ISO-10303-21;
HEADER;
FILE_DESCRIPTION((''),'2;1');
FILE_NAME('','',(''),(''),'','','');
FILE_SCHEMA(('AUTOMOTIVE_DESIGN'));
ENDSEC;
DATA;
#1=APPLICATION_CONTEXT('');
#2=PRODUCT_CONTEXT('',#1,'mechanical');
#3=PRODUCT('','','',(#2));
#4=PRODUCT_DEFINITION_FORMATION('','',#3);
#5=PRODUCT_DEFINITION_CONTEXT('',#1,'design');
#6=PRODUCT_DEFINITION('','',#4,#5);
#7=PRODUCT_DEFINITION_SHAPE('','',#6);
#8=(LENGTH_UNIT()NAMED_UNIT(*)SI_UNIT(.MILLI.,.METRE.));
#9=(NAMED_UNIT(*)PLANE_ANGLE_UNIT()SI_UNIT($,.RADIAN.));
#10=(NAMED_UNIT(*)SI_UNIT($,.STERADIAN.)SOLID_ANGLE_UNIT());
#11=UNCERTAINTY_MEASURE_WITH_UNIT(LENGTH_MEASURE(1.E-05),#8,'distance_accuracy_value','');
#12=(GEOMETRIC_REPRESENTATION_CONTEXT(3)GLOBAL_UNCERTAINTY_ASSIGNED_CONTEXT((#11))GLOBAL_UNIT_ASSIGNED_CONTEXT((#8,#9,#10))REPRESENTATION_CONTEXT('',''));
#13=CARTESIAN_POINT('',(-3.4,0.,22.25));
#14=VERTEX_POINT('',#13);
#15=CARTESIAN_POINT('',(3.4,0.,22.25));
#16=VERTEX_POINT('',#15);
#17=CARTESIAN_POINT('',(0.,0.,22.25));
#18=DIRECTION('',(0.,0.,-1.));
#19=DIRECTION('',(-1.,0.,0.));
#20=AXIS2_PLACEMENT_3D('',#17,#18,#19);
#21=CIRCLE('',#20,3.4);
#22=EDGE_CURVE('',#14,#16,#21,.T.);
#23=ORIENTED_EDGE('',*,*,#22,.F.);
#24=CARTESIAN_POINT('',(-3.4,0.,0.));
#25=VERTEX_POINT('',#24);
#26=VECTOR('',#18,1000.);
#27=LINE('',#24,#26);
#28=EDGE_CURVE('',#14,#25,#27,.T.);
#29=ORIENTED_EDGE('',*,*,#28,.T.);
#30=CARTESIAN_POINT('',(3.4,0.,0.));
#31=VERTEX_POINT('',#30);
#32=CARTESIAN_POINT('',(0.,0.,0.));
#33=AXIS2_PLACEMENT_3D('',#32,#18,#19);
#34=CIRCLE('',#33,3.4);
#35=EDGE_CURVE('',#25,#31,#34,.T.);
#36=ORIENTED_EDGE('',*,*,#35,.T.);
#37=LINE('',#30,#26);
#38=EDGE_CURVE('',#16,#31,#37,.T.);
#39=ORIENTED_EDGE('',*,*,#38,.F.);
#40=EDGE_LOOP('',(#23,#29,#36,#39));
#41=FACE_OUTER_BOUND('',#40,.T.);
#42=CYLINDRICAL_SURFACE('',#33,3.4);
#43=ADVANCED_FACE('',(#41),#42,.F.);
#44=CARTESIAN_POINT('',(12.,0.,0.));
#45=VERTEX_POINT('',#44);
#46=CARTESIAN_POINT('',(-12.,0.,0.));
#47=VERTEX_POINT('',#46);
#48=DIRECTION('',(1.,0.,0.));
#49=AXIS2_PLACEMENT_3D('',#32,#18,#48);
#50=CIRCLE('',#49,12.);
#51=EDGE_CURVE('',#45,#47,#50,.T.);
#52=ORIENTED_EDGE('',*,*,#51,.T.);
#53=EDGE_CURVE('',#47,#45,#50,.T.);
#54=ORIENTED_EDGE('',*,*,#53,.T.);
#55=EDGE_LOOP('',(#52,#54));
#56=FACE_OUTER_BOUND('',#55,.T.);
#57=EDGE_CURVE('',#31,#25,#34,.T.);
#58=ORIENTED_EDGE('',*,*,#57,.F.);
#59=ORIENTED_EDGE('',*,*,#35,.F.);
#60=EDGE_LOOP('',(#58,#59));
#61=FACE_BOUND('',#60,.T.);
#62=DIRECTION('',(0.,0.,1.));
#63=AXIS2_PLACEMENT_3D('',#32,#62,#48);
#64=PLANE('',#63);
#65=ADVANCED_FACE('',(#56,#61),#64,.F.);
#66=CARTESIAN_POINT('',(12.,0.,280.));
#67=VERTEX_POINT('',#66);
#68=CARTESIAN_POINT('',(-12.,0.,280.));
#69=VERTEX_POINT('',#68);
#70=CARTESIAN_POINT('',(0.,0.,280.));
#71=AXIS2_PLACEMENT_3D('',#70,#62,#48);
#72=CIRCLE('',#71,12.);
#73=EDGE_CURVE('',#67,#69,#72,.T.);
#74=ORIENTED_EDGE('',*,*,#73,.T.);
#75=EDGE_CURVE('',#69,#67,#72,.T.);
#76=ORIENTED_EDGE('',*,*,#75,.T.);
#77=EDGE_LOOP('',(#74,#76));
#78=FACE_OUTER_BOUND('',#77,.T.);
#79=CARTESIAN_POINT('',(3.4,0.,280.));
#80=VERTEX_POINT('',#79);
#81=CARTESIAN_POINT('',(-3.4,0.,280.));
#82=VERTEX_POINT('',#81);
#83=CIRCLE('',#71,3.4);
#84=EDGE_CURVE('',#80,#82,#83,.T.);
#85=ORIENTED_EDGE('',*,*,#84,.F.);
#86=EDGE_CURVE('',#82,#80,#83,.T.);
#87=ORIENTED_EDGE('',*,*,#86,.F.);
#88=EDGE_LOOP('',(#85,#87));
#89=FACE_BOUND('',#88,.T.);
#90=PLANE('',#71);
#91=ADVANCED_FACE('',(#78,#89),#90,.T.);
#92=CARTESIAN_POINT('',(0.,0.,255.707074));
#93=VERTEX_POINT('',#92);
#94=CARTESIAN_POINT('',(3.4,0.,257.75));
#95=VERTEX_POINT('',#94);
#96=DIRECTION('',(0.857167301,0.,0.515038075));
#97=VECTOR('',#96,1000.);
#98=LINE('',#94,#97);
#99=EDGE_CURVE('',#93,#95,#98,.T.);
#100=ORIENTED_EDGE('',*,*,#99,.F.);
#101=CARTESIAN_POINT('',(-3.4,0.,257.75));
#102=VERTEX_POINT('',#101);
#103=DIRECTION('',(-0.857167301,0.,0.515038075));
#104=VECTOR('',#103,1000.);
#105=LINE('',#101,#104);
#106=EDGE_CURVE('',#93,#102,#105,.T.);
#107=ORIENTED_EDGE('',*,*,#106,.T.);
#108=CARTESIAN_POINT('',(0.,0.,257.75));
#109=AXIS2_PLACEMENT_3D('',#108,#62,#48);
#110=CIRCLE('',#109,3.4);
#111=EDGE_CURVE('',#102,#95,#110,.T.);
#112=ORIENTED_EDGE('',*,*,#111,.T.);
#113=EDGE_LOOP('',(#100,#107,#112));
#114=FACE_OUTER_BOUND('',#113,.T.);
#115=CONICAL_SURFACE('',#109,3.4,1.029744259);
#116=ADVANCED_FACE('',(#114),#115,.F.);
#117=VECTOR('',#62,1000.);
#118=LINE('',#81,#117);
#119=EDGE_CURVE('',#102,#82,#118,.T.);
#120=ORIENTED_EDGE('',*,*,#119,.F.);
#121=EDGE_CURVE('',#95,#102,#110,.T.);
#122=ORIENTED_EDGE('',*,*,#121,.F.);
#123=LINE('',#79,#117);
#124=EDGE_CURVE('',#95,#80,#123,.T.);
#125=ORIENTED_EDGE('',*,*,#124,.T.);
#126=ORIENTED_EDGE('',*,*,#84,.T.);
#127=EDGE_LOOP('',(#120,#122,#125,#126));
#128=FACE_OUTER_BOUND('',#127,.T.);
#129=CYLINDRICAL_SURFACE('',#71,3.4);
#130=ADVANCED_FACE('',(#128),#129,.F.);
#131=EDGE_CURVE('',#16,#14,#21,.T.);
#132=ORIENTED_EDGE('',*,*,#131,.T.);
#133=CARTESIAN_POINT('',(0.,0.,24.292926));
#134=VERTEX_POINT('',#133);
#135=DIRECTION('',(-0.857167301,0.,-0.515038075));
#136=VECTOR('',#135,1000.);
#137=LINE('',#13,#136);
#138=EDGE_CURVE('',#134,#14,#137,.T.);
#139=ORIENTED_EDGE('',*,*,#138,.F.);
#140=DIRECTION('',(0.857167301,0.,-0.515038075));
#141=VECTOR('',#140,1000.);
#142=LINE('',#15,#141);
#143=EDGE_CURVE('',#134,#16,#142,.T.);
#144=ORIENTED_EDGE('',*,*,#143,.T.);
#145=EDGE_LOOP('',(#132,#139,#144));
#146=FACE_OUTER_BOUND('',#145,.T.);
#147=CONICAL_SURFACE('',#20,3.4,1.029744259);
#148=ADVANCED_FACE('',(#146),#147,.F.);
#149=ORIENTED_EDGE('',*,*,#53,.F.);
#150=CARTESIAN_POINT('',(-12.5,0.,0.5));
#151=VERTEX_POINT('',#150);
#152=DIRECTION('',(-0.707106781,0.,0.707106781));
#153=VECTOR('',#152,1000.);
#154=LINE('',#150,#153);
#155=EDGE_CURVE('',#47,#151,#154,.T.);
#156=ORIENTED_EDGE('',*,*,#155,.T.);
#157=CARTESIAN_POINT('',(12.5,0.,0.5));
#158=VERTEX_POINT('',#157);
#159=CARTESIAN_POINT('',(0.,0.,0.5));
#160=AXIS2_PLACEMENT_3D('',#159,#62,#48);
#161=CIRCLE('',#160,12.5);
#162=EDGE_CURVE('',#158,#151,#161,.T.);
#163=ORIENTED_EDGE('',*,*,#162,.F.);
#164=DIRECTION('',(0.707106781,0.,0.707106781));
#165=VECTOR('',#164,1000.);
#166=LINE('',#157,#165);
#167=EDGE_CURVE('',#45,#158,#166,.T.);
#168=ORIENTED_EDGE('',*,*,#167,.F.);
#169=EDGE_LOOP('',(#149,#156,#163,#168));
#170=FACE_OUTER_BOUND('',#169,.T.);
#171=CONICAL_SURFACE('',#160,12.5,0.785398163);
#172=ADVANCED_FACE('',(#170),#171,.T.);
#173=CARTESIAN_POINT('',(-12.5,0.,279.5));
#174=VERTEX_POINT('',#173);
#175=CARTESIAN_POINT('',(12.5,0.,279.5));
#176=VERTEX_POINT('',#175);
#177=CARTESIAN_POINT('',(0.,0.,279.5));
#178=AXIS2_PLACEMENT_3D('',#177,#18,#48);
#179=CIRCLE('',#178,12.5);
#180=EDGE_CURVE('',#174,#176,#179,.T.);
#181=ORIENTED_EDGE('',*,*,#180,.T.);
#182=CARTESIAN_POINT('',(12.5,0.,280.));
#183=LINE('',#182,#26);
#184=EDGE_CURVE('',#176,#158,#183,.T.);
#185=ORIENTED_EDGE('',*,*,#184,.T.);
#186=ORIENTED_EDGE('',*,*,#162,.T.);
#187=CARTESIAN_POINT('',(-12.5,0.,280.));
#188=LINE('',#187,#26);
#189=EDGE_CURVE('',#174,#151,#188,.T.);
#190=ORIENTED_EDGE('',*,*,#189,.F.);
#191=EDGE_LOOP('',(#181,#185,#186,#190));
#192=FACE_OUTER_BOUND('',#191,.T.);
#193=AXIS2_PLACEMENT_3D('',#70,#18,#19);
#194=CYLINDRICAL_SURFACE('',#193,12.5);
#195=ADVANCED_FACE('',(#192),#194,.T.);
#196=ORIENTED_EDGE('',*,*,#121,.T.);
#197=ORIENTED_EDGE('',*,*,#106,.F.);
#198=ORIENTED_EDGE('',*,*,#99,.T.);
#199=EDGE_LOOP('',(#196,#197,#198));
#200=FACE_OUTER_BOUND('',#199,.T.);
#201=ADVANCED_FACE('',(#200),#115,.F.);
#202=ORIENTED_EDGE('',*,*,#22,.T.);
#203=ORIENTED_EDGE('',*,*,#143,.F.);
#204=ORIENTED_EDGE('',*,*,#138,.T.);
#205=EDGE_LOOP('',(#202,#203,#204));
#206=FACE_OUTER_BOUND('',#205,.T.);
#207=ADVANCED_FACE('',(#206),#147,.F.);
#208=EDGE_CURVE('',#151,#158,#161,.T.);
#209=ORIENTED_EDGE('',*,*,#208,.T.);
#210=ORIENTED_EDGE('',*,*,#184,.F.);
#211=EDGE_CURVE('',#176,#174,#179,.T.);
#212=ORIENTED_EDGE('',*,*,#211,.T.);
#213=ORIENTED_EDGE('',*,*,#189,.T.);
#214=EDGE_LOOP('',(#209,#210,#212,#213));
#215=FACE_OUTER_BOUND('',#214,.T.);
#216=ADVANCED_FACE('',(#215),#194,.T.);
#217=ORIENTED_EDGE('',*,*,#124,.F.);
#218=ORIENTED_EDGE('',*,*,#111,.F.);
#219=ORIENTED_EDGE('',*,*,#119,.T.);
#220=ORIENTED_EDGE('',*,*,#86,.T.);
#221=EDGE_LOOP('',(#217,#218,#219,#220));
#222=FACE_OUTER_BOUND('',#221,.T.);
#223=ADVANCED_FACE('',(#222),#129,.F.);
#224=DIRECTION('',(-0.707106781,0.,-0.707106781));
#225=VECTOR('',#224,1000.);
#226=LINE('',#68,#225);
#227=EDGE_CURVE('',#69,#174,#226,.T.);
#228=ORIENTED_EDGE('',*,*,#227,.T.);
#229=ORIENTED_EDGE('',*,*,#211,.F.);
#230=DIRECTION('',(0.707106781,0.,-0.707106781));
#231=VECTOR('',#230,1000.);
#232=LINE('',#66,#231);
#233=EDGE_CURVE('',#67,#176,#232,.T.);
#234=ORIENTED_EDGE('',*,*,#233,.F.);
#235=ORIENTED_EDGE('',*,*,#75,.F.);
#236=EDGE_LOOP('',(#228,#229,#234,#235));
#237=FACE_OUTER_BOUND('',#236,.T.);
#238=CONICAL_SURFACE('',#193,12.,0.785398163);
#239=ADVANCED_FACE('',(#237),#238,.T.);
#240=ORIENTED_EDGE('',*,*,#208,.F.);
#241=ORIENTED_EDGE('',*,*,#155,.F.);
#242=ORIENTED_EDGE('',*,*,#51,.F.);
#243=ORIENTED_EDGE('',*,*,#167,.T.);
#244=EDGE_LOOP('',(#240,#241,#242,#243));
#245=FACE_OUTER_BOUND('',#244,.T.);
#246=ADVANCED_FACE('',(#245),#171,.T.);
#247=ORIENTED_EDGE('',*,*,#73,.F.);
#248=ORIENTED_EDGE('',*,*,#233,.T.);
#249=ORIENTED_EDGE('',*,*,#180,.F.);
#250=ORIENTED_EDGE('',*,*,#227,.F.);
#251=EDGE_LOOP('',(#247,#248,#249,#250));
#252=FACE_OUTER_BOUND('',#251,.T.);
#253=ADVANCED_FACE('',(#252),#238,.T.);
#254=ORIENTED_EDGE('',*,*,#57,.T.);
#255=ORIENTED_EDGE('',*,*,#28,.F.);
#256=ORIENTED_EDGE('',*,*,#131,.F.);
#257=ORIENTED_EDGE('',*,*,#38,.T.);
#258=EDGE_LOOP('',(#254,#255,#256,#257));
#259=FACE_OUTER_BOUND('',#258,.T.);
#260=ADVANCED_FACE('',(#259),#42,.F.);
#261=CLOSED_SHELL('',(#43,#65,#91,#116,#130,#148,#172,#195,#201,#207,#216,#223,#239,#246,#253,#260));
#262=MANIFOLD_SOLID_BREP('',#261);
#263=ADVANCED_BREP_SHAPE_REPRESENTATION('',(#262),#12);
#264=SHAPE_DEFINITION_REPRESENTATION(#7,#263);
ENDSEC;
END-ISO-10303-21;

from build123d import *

# Parameters (mm, degrees)
SKETCH_1_R             = 12.5
EXTRUDE_1_DEPTH        = 280
HOLE_WIZARD_M8_1_D     = 6.8
HOLE_WIZARD_M8_1_DEPTH = 22.25
HOLE_WIZARD_M8_1_TIP   = 2.042926105
HOLE_WIZARD_M8_2_D     = 6.8
HOLE_WIZARD_M8_2_DEPTH = 22.25
HOLE_WIZARD_M8_2_TIP   = 2.042926105
CHAMFER_1_SIZE         = 0.5


with BuildPart() as part:
    # 草图1 → 凸台-拉伸1 (new body)
    with BuildSketch(Plane.XY):
        Circle(SKETCH_1_R)
    extrude(amount=EXTRUDE_1_DEPTH)

    # M8 螺纹孔1
    with Locations(Plane.XY.offset(280)):
        with Locations((0, 0)):
            Hole(HOLE_WIZARD_M8_1_D / 2, depth=HOLE_WIZARD_M8_1_DEPTH)
            with Locations((0, 0, -(HOLE_WIZARD_M8_1_DEPTH + HOLE_WIZARD_M8_1_TIP / 2))):  # 118° drill point
                Cone(0, HOLE_WIZARD_M8_1_D / 2, HOLE_WIZARD_M8_1_TIP, mode=Mode.SUBTRACT)

    # M8 螺纹孔2
    with Locations(Plane(origin=(0, 0, 0), x_dir=(-1, 0, 0), z_dir=(0, 0, -1))):
        with Locations((0, 0)):
            Hole(HOLE_WIZARD_M8_2_D / 2, depth=HOLE_WIZARD_M8_2_DEPTH)
            with Locations((0, 0, -(HOLE_WIZARD_M8_2_DEPTH + HOLE_WIZARD_M8_2_TIP / 2))):  # 118° drill point
                Cone(0, HOLE_WIZARD_M8_2_D / 2, HOLE_WIZARD_M8_2_TIP, mode=Mode.SUBTRACT)

    # 倒角1
    chamfer_1_edges = [part.edges().sort_by_distance(p)[0] for p in [
        (-12.5, 0, 0),
        (-12.5, 0, 280),
    ]]
    chamfer(chamfer_1_edges, length=CHAMFER_1_SIZE)


solid = part.part
